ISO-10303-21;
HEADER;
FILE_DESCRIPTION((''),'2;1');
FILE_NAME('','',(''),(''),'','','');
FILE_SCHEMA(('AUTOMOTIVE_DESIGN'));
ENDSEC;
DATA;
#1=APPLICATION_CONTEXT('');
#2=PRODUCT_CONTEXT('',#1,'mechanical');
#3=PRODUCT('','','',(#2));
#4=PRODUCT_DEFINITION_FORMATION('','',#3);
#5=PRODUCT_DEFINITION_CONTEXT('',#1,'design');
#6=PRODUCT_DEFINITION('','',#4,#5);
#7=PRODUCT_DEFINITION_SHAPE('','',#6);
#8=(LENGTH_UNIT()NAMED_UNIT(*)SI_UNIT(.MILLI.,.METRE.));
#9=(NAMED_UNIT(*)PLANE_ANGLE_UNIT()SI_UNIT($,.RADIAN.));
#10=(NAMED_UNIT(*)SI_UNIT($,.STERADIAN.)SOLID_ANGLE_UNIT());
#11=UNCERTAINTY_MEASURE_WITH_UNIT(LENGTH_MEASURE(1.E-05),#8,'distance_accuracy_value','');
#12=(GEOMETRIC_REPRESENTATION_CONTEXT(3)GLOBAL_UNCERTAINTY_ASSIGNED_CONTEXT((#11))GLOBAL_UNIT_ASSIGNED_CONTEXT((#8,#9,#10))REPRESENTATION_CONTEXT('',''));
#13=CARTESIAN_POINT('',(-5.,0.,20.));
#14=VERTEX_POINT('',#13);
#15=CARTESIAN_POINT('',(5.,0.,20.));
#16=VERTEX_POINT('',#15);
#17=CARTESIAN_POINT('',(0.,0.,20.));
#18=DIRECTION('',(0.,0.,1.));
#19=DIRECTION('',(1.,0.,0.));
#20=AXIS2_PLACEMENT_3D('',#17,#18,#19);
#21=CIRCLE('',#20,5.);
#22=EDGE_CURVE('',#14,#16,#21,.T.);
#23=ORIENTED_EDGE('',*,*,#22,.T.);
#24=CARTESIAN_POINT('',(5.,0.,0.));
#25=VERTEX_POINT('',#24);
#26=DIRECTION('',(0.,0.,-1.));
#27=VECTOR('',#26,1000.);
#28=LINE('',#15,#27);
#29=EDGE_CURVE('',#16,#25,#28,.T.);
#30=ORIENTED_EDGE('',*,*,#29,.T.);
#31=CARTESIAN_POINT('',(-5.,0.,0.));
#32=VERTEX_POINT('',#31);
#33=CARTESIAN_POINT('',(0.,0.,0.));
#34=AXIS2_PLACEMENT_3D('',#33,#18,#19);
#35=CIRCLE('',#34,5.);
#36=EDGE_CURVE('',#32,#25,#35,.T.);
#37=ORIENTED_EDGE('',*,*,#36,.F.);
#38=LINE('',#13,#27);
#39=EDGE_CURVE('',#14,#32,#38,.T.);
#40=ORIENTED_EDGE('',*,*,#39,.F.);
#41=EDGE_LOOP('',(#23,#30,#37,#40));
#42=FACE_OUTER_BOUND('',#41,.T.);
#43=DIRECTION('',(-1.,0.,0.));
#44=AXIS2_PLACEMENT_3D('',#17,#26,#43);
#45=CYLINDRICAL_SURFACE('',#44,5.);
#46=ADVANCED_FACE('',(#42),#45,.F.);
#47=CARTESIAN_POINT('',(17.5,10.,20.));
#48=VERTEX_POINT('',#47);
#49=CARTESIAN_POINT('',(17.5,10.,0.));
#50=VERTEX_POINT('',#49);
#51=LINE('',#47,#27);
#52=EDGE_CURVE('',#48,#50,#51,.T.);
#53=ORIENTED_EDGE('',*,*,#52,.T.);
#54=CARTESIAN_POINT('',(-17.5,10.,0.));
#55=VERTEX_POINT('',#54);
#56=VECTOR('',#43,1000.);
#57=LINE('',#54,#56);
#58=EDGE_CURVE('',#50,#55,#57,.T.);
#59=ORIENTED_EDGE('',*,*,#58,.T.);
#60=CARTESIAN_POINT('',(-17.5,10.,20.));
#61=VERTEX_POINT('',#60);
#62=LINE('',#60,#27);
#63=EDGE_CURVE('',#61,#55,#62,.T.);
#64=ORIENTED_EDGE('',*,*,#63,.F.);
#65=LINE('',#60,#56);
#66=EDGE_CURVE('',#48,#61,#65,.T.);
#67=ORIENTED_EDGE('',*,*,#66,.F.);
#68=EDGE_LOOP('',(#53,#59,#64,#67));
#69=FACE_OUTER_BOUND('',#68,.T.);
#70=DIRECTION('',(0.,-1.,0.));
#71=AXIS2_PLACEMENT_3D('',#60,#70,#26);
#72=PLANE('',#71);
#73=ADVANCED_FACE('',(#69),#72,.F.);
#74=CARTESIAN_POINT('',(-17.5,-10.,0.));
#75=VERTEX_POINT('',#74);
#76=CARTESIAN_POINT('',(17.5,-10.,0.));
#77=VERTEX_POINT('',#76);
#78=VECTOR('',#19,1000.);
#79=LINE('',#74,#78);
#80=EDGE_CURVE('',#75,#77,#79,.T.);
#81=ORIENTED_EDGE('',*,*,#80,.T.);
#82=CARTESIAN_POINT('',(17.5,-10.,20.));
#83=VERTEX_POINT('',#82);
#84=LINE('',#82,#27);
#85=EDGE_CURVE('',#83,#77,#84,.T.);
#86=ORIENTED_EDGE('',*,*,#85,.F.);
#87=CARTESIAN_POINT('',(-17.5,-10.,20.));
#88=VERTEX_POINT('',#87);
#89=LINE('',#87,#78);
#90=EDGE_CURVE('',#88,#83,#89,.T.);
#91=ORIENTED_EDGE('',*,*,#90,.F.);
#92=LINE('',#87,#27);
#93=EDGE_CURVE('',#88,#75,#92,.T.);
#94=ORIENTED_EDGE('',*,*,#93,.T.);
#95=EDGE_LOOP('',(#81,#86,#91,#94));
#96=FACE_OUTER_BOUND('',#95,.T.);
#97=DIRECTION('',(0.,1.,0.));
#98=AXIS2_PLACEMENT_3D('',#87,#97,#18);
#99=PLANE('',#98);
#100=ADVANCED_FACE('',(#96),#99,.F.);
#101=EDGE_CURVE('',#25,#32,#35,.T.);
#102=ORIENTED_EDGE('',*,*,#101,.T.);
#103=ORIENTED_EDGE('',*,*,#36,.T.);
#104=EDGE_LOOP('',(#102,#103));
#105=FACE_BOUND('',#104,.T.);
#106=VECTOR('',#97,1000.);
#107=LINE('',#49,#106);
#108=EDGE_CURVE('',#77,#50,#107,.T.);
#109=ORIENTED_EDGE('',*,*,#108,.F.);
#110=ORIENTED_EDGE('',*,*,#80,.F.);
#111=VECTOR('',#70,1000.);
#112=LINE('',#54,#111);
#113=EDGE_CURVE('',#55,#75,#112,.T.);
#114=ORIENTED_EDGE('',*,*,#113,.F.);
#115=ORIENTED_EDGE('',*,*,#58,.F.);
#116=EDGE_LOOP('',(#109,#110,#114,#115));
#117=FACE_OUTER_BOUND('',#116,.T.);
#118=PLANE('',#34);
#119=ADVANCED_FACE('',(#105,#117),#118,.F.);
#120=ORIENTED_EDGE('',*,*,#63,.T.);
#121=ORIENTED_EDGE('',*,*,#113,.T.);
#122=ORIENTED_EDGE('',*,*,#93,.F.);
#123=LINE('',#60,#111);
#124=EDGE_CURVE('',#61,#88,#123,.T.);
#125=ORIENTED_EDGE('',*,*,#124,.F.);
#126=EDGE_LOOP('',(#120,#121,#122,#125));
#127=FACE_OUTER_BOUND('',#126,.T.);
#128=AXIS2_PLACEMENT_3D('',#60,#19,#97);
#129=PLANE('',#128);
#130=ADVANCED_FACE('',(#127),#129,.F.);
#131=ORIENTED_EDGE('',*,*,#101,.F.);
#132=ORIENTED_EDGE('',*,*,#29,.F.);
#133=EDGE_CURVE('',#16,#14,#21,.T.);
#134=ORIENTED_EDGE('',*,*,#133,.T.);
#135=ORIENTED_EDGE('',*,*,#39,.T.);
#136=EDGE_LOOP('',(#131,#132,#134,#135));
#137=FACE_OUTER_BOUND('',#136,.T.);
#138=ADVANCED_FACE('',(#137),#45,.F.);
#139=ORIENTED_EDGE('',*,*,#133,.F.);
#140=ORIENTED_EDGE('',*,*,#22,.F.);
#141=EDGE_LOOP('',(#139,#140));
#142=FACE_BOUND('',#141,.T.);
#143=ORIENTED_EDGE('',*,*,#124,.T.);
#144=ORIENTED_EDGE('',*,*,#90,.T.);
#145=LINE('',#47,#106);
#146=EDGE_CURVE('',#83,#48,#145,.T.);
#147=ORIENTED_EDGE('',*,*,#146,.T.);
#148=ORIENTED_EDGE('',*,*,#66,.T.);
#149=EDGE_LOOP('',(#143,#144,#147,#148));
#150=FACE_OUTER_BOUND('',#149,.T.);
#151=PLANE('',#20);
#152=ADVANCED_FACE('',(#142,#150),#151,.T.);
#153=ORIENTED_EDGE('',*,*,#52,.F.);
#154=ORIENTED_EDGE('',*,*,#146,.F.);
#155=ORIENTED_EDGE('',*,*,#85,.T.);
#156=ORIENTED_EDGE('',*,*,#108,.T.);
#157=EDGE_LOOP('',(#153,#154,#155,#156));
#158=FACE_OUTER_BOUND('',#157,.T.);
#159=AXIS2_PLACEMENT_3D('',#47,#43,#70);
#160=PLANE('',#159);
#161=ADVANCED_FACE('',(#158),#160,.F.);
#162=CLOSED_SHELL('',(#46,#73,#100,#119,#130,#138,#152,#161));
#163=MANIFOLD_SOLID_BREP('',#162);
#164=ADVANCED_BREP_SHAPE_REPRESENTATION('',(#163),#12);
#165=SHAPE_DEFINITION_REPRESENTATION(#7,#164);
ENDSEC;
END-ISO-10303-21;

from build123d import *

# Parameters (mm, degrees)
SKETCH1_W           = 35
SKETCH1_H           = 20
SKETCH1_R           = 5
BOSS_EXTRUDE1_DEPTH = 20


with BuildPart() as part:
    # Sketch1 → Boss-Extrude1 (new body)
    with BuildSketch(Plane.XY):
        Rectangle(SKETCH1_W, SKETCH1_H)
        Circle(SKETCH1_R, mode=Mode.SUBTRACT)
    extrude(amount=BOSS_EXTRUDE1_DEPTH)


solid = part.part
